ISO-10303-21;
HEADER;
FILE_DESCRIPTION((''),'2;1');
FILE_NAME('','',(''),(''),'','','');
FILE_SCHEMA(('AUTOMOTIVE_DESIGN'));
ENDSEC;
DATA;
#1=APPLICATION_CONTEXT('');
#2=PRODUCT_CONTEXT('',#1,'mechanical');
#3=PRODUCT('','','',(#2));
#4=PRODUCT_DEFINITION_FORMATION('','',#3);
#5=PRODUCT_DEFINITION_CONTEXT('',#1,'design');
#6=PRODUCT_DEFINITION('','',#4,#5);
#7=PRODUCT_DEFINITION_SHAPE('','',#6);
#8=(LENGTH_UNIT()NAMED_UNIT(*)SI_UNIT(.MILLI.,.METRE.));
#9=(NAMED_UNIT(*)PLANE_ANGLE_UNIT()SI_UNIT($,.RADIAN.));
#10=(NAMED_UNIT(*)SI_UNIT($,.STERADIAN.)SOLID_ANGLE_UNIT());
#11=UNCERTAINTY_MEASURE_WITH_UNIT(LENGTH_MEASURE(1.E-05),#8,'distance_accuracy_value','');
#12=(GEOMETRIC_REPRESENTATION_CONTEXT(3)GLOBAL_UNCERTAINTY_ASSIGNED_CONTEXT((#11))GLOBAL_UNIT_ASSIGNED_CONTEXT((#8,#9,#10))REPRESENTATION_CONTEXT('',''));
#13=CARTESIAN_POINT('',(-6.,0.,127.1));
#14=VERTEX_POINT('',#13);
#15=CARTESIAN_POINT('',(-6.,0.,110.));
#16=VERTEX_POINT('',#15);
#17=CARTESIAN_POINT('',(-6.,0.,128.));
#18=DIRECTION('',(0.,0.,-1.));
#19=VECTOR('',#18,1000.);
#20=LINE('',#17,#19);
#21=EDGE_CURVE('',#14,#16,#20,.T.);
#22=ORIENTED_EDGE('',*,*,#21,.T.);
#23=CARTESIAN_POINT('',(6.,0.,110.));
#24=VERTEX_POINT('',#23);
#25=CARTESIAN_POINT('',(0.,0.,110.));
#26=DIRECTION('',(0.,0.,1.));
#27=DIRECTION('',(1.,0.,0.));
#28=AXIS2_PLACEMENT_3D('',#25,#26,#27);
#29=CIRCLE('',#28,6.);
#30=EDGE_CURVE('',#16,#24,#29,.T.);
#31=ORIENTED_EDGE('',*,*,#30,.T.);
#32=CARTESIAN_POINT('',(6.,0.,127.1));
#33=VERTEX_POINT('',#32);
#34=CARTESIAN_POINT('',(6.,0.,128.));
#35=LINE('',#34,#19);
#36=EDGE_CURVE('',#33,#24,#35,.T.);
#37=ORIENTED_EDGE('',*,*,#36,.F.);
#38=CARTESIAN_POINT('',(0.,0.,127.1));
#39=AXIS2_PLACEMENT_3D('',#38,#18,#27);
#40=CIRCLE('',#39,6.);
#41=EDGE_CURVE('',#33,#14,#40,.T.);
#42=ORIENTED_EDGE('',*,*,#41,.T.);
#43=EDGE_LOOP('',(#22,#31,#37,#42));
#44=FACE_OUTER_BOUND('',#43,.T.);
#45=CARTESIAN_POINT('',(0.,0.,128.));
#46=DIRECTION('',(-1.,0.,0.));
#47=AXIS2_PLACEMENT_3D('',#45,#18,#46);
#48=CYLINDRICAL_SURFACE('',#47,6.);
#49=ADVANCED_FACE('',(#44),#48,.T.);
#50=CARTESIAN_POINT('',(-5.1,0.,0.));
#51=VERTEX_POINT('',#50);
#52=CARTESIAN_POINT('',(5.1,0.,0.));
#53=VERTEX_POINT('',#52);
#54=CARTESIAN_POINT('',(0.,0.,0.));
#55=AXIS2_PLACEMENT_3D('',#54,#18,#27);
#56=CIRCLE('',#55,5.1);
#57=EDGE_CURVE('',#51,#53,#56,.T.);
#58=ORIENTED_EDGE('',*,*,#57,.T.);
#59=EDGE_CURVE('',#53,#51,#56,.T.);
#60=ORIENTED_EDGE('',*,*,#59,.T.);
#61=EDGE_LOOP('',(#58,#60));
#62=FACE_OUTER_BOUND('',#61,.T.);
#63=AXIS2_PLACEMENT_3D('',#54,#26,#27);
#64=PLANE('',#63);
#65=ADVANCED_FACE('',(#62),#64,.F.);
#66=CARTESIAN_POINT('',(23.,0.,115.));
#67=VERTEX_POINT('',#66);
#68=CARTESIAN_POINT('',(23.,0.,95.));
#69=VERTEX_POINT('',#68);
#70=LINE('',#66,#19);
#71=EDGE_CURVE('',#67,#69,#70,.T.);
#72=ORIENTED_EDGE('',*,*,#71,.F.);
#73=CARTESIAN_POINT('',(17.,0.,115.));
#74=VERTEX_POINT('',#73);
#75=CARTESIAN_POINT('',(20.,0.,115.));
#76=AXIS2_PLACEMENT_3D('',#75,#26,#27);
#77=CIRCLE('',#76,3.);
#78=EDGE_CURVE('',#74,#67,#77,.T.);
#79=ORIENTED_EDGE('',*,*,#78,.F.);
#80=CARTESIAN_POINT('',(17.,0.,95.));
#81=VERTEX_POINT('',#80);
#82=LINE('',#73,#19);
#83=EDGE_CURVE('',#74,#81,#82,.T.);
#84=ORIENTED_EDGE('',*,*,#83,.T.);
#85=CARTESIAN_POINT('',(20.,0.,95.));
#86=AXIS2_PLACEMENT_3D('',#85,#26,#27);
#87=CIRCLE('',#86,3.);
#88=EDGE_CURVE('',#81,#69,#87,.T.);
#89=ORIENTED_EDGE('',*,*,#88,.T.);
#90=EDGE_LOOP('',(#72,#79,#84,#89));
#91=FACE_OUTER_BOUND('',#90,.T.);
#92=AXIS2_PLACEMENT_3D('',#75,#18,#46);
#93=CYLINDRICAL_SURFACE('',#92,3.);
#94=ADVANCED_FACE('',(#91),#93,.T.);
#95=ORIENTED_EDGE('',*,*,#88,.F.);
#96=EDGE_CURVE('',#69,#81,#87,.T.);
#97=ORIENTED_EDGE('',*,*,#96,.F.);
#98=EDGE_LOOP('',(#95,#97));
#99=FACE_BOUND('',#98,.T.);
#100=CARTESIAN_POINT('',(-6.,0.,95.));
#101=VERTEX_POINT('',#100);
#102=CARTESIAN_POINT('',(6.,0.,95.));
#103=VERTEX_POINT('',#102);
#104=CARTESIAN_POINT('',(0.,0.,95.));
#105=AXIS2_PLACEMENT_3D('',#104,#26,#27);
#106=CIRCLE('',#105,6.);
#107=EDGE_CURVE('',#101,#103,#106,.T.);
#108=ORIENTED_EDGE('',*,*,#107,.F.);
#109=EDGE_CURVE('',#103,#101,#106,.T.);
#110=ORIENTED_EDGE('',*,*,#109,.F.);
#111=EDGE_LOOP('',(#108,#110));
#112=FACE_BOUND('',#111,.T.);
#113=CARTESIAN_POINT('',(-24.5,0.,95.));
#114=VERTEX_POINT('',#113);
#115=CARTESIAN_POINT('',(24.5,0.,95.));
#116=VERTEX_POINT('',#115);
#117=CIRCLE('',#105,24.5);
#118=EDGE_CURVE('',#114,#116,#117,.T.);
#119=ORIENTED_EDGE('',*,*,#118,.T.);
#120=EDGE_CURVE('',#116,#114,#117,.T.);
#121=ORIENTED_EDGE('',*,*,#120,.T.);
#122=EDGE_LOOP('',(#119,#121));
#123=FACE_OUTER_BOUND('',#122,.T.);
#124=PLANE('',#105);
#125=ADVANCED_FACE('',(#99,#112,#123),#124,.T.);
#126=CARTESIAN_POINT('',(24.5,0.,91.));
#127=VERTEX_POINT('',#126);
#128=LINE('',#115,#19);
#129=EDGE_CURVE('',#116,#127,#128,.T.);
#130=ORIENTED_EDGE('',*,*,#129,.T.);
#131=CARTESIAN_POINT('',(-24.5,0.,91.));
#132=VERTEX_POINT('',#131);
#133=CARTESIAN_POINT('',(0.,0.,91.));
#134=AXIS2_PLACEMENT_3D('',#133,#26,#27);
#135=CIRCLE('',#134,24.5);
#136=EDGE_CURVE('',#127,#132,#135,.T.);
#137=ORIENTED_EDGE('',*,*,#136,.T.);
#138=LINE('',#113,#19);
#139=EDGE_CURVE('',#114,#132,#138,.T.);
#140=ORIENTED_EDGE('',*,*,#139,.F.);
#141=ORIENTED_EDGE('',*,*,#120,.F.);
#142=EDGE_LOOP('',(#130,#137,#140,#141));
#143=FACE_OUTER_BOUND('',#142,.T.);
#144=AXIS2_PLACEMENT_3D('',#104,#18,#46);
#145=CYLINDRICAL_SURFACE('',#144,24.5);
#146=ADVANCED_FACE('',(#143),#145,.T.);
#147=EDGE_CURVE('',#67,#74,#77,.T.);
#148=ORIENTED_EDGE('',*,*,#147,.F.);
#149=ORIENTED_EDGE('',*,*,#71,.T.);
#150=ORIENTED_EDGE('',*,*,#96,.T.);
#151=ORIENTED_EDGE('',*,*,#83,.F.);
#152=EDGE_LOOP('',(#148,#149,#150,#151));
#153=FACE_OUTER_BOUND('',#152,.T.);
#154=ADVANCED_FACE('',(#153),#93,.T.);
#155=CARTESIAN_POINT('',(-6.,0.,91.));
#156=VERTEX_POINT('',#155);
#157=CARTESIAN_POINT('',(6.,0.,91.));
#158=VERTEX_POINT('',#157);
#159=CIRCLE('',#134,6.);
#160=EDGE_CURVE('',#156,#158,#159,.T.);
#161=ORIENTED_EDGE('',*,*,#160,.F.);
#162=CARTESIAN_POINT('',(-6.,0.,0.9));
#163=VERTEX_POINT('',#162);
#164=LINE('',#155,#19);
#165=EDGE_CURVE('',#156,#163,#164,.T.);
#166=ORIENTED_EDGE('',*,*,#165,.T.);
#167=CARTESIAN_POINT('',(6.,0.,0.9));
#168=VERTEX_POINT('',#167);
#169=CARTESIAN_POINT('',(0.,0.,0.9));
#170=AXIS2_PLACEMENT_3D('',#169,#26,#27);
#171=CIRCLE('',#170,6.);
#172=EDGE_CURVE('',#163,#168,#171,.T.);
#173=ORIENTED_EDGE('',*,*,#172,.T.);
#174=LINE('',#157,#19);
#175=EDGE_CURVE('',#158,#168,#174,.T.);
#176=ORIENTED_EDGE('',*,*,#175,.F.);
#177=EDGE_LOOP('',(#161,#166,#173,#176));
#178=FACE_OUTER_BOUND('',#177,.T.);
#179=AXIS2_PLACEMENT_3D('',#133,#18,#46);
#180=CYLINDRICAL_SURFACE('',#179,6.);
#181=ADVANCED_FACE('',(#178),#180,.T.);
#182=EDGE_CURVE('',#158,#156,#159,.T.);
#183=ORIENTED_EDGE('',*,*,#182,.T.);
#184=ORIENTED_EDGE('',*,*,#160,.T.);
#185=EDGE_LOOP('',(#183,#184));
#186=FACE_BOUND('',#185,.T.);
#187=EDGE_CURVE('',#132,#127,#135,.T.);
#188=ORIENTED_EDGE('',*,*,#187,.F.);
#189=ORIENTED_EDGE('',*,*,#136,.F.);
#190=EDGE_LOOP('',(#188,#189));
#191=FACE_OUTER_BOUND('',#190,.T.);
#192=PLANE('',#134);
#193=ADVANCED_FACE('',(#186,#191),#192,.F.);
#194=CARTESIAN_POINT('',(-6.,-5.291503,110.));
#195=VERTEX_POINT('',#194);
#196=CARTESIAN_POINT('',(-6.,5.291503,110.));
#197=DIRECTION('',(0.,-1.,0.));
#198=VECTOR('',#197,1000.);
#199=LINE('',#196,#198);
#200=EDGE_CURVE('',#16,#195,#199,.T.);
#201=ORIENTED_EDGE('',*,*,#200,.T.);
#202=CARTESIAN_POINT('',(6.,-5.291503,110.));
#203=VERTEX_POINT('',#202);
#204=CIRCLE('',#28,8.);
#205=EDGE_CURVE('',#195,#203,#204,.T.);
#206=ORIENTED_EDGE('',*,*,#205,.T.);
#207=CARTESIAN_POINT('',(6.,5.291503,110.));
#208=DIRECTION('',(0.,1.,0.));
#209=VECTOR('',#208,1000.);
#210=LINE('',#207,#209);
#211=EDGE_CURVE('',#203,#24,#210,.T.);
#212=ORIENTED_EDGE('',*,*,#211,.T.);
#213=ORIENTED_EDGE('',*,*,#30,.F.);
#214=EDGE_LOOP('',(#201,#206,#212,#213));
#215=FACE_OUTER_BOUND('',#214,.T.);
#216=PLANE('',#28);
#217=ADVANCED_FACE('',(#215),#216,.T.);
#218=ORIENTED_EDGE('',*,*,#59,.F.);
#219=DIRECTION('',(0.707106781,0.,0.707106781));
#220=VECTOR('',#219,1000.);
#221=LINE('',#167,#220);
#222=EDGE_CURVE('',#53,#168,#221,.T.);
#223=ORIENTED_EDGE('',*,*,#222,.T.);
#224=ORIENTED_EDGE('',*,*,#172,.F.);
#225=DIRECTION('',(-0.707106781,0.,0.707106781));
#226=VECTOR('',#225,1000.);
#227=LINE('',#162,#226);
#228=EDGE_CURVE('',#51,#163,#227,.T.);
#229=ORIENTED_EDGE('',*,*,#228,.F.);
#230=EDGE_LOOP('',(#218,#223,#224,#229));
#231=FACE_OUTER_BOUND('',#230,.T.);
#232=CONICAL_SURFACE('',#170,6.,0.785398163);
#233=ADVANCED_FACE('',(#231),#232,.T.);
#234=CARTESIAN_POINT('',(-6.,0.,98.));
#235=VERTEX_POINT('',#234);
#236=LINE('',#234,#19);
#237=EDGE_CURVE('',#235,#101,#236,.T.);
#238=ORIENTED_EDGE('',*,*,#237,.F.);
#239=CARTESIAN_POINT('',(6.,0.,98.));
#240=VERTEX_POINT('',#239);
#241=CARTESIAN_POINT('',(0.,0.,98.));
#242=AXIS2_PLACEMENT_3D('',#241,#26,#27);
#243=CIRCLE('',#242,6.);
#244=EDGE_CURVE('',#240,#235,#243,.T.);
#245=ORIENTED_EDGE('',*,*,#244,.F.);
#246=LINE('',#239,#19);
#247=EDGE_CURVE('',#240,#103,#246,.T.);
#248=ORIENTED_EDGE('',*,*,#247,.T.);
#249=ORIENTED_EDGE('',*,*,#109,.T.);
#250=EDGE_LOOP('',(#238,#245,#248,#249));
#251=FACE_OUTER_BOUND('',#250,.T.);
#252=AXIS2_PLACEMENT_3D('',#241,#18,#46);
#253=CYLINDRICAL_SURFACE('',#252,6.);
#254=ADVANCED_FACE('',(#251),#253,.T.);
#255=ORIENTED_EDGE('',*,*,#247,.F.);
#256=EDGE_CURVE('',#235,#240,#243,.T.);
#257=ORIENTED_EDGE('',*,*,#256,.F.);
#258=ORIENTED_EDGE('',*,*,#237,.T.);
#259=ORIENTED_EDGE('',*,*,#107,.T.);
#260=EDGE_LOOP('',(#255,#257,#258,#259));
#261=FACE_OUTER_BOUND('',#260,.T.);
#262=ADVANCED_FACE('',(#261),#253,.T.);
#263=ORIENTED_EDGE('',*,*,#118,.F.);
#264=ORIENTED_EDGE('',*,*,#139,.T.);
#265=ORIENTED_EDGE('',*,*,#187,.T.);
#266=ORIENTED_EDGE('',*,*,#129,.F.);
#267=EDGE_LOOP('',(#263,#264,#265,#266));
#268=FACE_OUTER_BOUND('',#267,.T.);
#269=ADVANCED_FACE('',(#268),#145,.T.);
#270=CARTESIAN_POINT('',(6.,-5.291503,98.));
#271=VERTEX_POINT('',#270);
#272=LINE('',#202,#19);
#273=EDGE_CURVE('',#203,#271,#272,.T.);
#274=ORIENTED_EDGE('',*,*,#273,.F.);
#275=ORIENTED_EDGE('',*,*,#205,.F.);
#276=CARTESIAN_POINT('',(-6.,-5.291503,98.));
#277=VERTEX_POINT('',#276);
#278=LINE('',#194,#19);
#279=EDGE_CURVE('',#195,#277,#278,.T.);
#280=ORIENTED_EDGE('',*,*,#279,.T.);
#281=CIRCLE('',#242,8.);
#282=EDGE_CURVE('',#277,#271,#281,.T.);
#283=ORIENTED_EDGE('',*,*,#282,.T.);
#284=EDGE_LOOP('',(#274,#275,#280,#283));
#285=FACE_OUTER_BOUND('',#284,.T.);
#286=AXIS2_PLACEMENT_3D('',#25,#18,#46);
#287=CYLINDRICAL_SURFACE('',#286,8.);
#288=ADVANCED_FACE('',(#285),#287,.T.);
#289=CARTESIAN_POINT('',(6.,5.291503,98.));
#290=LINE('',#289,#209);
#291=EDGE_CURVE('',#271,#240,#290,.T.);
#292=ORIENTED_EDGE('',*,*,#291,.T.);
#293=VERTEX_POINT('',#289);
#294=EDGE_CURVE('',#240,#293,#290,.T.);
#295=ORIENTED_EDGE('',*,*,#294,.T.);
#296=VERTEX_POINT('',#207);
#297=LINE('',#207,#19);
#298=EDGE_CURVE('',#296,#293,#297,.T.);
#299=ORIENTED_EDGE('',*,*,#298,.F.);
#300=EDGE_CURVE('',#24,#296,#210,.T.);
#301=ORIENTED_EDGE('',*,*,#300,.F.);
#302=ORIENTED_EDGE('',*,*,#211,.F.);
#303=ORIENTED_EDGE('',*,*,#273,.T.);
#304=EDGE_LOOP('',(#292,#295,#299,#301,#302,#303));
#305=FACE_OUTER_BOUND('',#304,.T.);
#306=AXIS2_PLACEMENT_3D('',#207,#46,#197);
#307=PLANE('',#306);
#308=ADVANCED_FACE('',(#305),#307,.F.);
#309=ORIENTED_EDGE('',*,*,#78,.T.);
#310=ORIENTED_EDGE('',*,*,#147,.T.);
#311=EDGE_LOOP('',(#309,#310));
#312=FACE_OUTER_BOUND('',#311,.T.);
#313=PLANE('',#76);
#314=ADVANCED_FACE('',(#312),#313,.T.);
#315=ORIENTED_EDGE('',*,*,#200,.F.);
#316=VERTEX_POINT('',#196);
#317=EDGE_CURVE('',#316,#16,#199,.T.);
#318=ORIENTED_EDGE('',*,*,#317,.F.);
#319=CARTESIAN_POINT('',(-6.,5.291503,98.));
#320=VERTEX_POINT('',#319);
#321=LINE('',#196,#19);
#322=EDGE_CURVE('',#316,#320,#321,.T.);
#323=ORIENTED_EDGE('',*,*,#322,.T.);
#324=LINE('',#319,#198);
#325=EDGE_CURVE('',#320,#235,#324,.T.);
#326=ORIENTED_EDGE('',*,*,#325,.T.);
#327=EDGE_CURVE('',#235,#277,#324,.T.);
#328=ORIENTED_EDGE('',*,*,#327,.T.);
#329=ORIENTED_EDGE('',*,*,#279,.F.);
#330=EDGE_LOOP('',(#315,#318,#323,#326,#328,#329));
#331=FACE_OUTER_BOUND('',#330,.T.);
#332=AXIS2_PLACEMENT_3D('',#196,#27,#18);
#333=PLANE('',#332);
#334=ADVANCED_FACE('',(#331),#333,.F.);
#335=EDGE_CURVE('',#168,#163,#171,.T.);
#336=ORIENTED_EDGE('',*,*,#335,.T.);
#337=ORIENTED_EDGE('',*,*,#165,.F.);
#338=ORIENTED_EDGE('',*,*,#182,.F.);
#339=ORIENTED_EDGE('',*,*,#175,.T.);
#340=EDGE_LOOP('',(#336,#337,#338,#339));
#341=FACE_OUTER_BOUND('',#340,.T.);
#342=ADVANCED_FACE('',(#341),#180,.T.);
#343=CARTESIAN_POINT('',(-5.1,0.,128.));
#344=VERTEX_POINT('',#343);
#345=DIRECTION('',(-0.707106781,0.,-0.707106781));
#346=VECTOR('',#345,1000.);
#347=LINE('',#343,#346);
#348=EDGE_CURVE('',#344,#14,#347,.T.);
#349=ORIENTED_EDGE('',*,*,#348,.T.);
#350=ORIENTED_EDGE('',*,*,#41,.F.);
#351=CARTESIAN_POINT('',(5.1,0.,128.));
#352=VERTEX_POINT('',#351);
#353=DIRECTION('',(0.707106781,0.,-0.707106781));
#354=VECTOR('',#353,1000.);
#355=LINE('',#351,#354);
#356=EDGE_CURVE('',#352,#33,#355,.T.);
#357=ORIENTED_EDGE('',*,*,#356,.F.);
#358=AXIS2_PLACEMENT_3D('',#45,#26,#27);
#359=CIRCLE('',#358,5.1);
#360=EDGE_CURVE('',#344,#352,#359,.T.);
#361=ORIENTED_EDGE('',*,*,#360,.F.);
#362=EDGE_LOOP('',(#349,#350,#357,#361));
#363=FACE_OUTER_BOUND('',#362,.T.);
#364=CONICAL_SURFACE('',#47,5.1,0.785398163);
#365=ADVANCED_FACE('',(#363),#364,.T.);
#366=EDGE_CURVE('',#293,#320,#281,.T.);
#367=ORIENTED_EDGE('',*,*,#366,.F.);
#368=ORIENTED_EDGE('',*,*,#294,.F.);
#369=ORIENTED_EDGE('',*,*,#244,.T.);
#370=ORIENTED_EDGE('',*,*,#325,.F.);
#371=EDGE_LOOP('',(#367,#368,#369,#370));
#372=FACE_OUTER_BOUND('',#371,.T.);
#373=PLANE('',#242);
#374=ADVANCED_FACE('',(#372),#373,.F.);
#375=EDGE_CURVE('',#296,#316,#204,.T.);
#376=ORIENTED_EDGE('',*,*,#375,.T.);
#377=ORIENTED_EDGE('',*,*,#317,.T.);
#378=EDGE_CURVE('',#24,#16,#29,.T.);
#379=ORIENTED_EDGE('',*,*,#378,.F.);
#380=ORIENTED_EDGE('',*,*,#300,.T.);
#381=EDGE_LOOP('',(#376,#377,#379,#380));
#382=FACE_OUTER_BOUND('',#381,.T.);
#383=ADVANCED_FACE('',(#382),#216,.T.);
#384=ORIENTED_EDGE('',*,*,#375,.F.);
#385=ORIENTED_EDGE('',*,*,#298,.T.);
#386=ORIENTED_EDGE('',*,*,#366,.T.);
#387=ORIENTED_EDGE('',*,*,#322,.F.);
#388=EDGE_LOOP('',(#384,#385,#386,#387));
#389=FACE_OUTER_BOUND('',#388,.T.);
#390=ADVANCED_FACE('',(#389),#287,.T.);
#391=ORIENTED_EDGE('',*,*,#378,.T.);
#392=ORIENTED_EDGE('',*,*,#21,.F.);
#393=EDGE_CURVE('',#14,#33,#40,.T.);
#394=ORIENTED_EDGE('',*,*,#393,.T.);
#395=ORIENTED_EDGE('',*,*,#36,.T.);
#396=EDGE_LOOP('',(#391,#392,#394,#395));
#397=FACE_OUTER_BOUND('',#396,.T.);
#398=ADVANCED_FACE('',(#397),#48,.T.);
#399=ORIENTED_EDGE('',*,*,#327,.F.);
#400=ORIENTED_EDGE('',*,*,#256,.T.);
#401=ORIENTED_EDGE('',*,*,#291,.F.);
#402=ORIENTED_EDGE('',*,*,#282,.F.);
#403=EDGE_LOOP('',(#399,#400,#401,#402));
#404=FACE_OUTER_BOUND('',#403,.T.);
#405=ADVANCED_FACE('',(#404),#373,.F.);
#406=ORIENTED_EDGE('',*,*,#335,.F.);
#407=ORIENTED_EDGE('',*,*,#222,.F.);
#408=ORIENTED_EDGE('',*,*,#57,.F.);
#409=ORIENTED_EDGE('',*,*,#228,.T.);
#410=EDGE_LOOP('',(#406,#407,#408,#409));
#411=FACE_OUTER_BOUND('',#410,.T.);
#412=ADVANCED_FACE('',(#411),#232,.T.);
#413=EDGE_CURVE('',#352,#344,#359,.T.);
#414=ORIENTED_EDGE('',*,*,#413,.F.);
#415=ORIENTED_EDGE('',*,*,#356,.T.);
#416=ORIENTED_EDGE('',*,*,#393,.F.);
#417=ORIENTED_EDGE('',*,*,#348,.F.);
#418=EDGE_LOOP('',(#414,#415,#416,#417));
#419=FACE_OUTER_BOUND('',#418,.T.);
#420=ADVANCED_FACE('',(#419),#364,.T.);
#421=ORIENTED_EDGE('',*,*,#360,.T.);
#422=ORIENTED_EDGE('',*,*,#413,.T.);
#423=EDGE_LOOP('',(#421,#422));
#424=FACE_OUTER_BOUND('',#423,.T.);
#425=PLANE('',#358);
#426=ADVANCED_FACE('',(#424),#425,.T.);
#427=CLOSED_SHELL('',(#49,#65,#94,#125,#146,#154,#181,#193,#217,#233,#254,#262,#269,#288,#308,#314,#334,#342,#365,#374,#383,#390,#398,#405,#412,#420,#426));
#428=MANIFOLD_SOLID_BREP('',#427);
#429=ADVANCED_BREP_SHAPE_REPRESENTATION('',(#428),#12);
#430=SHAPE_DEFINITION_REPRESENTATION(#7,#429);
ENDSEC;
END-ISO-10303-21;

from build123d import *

# Parameters (mm, degrees)
SKETCH1_R           = 6
BOSS_EXTRUDE1_DEPTH = 91
SKETCH2_R           = 24.5
BOSS_EXTRUDE2_DEPTH = 4
SKETCH3_R           = 6
BOSS_EXTRUDE3_DEPTH = 3
BOSS_EXTRUDE4_DEPTH = 12
SKETCH5_R           = 6
BOSS_EXTRUDE5_DEPTH = 18
CHAMFER1_SIZE       = 0.9
SKETCH6_R           = 3
BOSS_EXTRUDE6_DEPTH = 20


with BuildPart() as part:
    # Sketch1 → Boss-Extrude1 (new body)
    with BuildSketch(Plane.XY):
        Circle(SKETCH1_R)
    extrude(amount=BOSS_EXTRUDE1_DEPTH)

    # Sketch2 → Boss-Extrude2 (add)
    with BuildSketch(Plane.XY.offset(91)):
        Circle(SKETCH2_R)
    extrude(amount=BOSS_EXTRUDE2_DEPTH)

    # Sketch3 → Boss-Extrude3 (add)
    with BuildSketch(Plane.XY.offset(95)):
        Circle(SKETCH3_R)
    extrude(amount=BOSS_EXTRUDE3_DEPTH)

    # Sketch4 → Boss-Extrude4 (add)
    with BuildSketch(Plane.XY.offset(98)):
        with BuildLine():
            Line((6, 5.291502622), (6, -5.291502622))
            ThreePointArc((6, -5.291502622), (0, -8), (-6, -5.291502622))
            Line((-6, -5.291502622), (-6, 5.291502622))
            ThreePointArc((-6, 5.291502622), (0, 8), (6, 5.291502622))
        make_face()
    extrude(amount=BOSS_EXTRUDE4_DEPTH)

    # Sketch5 → Boss-Extrude5 (add)
    with BuildSketch(Plane.XY.offset(110)):
        Circle(SKETCH5_R)
    extrude(amount=BOSS_EXTRUDE5_DEPTH)

    # Chamfer1
    chamfer1_edges = [part.edges().sort_by_distance(p)[0] for p in [
        (-6, 0, 0),
        (-6, 0, 128),
    ]]
    chamfer(chamfer1_edges, length=CHAMFER1_SIZE)

    # Sketch6 → Boss-Extrude6 (add)
    with BuildSketch(Plane.XY.offset(95)):
        with Locations((20, 0)):
            Circle(SKETCH6_R)
    extrude(amount=BOSS_EXTRUDE6_DEPTH)


solid = part.part
